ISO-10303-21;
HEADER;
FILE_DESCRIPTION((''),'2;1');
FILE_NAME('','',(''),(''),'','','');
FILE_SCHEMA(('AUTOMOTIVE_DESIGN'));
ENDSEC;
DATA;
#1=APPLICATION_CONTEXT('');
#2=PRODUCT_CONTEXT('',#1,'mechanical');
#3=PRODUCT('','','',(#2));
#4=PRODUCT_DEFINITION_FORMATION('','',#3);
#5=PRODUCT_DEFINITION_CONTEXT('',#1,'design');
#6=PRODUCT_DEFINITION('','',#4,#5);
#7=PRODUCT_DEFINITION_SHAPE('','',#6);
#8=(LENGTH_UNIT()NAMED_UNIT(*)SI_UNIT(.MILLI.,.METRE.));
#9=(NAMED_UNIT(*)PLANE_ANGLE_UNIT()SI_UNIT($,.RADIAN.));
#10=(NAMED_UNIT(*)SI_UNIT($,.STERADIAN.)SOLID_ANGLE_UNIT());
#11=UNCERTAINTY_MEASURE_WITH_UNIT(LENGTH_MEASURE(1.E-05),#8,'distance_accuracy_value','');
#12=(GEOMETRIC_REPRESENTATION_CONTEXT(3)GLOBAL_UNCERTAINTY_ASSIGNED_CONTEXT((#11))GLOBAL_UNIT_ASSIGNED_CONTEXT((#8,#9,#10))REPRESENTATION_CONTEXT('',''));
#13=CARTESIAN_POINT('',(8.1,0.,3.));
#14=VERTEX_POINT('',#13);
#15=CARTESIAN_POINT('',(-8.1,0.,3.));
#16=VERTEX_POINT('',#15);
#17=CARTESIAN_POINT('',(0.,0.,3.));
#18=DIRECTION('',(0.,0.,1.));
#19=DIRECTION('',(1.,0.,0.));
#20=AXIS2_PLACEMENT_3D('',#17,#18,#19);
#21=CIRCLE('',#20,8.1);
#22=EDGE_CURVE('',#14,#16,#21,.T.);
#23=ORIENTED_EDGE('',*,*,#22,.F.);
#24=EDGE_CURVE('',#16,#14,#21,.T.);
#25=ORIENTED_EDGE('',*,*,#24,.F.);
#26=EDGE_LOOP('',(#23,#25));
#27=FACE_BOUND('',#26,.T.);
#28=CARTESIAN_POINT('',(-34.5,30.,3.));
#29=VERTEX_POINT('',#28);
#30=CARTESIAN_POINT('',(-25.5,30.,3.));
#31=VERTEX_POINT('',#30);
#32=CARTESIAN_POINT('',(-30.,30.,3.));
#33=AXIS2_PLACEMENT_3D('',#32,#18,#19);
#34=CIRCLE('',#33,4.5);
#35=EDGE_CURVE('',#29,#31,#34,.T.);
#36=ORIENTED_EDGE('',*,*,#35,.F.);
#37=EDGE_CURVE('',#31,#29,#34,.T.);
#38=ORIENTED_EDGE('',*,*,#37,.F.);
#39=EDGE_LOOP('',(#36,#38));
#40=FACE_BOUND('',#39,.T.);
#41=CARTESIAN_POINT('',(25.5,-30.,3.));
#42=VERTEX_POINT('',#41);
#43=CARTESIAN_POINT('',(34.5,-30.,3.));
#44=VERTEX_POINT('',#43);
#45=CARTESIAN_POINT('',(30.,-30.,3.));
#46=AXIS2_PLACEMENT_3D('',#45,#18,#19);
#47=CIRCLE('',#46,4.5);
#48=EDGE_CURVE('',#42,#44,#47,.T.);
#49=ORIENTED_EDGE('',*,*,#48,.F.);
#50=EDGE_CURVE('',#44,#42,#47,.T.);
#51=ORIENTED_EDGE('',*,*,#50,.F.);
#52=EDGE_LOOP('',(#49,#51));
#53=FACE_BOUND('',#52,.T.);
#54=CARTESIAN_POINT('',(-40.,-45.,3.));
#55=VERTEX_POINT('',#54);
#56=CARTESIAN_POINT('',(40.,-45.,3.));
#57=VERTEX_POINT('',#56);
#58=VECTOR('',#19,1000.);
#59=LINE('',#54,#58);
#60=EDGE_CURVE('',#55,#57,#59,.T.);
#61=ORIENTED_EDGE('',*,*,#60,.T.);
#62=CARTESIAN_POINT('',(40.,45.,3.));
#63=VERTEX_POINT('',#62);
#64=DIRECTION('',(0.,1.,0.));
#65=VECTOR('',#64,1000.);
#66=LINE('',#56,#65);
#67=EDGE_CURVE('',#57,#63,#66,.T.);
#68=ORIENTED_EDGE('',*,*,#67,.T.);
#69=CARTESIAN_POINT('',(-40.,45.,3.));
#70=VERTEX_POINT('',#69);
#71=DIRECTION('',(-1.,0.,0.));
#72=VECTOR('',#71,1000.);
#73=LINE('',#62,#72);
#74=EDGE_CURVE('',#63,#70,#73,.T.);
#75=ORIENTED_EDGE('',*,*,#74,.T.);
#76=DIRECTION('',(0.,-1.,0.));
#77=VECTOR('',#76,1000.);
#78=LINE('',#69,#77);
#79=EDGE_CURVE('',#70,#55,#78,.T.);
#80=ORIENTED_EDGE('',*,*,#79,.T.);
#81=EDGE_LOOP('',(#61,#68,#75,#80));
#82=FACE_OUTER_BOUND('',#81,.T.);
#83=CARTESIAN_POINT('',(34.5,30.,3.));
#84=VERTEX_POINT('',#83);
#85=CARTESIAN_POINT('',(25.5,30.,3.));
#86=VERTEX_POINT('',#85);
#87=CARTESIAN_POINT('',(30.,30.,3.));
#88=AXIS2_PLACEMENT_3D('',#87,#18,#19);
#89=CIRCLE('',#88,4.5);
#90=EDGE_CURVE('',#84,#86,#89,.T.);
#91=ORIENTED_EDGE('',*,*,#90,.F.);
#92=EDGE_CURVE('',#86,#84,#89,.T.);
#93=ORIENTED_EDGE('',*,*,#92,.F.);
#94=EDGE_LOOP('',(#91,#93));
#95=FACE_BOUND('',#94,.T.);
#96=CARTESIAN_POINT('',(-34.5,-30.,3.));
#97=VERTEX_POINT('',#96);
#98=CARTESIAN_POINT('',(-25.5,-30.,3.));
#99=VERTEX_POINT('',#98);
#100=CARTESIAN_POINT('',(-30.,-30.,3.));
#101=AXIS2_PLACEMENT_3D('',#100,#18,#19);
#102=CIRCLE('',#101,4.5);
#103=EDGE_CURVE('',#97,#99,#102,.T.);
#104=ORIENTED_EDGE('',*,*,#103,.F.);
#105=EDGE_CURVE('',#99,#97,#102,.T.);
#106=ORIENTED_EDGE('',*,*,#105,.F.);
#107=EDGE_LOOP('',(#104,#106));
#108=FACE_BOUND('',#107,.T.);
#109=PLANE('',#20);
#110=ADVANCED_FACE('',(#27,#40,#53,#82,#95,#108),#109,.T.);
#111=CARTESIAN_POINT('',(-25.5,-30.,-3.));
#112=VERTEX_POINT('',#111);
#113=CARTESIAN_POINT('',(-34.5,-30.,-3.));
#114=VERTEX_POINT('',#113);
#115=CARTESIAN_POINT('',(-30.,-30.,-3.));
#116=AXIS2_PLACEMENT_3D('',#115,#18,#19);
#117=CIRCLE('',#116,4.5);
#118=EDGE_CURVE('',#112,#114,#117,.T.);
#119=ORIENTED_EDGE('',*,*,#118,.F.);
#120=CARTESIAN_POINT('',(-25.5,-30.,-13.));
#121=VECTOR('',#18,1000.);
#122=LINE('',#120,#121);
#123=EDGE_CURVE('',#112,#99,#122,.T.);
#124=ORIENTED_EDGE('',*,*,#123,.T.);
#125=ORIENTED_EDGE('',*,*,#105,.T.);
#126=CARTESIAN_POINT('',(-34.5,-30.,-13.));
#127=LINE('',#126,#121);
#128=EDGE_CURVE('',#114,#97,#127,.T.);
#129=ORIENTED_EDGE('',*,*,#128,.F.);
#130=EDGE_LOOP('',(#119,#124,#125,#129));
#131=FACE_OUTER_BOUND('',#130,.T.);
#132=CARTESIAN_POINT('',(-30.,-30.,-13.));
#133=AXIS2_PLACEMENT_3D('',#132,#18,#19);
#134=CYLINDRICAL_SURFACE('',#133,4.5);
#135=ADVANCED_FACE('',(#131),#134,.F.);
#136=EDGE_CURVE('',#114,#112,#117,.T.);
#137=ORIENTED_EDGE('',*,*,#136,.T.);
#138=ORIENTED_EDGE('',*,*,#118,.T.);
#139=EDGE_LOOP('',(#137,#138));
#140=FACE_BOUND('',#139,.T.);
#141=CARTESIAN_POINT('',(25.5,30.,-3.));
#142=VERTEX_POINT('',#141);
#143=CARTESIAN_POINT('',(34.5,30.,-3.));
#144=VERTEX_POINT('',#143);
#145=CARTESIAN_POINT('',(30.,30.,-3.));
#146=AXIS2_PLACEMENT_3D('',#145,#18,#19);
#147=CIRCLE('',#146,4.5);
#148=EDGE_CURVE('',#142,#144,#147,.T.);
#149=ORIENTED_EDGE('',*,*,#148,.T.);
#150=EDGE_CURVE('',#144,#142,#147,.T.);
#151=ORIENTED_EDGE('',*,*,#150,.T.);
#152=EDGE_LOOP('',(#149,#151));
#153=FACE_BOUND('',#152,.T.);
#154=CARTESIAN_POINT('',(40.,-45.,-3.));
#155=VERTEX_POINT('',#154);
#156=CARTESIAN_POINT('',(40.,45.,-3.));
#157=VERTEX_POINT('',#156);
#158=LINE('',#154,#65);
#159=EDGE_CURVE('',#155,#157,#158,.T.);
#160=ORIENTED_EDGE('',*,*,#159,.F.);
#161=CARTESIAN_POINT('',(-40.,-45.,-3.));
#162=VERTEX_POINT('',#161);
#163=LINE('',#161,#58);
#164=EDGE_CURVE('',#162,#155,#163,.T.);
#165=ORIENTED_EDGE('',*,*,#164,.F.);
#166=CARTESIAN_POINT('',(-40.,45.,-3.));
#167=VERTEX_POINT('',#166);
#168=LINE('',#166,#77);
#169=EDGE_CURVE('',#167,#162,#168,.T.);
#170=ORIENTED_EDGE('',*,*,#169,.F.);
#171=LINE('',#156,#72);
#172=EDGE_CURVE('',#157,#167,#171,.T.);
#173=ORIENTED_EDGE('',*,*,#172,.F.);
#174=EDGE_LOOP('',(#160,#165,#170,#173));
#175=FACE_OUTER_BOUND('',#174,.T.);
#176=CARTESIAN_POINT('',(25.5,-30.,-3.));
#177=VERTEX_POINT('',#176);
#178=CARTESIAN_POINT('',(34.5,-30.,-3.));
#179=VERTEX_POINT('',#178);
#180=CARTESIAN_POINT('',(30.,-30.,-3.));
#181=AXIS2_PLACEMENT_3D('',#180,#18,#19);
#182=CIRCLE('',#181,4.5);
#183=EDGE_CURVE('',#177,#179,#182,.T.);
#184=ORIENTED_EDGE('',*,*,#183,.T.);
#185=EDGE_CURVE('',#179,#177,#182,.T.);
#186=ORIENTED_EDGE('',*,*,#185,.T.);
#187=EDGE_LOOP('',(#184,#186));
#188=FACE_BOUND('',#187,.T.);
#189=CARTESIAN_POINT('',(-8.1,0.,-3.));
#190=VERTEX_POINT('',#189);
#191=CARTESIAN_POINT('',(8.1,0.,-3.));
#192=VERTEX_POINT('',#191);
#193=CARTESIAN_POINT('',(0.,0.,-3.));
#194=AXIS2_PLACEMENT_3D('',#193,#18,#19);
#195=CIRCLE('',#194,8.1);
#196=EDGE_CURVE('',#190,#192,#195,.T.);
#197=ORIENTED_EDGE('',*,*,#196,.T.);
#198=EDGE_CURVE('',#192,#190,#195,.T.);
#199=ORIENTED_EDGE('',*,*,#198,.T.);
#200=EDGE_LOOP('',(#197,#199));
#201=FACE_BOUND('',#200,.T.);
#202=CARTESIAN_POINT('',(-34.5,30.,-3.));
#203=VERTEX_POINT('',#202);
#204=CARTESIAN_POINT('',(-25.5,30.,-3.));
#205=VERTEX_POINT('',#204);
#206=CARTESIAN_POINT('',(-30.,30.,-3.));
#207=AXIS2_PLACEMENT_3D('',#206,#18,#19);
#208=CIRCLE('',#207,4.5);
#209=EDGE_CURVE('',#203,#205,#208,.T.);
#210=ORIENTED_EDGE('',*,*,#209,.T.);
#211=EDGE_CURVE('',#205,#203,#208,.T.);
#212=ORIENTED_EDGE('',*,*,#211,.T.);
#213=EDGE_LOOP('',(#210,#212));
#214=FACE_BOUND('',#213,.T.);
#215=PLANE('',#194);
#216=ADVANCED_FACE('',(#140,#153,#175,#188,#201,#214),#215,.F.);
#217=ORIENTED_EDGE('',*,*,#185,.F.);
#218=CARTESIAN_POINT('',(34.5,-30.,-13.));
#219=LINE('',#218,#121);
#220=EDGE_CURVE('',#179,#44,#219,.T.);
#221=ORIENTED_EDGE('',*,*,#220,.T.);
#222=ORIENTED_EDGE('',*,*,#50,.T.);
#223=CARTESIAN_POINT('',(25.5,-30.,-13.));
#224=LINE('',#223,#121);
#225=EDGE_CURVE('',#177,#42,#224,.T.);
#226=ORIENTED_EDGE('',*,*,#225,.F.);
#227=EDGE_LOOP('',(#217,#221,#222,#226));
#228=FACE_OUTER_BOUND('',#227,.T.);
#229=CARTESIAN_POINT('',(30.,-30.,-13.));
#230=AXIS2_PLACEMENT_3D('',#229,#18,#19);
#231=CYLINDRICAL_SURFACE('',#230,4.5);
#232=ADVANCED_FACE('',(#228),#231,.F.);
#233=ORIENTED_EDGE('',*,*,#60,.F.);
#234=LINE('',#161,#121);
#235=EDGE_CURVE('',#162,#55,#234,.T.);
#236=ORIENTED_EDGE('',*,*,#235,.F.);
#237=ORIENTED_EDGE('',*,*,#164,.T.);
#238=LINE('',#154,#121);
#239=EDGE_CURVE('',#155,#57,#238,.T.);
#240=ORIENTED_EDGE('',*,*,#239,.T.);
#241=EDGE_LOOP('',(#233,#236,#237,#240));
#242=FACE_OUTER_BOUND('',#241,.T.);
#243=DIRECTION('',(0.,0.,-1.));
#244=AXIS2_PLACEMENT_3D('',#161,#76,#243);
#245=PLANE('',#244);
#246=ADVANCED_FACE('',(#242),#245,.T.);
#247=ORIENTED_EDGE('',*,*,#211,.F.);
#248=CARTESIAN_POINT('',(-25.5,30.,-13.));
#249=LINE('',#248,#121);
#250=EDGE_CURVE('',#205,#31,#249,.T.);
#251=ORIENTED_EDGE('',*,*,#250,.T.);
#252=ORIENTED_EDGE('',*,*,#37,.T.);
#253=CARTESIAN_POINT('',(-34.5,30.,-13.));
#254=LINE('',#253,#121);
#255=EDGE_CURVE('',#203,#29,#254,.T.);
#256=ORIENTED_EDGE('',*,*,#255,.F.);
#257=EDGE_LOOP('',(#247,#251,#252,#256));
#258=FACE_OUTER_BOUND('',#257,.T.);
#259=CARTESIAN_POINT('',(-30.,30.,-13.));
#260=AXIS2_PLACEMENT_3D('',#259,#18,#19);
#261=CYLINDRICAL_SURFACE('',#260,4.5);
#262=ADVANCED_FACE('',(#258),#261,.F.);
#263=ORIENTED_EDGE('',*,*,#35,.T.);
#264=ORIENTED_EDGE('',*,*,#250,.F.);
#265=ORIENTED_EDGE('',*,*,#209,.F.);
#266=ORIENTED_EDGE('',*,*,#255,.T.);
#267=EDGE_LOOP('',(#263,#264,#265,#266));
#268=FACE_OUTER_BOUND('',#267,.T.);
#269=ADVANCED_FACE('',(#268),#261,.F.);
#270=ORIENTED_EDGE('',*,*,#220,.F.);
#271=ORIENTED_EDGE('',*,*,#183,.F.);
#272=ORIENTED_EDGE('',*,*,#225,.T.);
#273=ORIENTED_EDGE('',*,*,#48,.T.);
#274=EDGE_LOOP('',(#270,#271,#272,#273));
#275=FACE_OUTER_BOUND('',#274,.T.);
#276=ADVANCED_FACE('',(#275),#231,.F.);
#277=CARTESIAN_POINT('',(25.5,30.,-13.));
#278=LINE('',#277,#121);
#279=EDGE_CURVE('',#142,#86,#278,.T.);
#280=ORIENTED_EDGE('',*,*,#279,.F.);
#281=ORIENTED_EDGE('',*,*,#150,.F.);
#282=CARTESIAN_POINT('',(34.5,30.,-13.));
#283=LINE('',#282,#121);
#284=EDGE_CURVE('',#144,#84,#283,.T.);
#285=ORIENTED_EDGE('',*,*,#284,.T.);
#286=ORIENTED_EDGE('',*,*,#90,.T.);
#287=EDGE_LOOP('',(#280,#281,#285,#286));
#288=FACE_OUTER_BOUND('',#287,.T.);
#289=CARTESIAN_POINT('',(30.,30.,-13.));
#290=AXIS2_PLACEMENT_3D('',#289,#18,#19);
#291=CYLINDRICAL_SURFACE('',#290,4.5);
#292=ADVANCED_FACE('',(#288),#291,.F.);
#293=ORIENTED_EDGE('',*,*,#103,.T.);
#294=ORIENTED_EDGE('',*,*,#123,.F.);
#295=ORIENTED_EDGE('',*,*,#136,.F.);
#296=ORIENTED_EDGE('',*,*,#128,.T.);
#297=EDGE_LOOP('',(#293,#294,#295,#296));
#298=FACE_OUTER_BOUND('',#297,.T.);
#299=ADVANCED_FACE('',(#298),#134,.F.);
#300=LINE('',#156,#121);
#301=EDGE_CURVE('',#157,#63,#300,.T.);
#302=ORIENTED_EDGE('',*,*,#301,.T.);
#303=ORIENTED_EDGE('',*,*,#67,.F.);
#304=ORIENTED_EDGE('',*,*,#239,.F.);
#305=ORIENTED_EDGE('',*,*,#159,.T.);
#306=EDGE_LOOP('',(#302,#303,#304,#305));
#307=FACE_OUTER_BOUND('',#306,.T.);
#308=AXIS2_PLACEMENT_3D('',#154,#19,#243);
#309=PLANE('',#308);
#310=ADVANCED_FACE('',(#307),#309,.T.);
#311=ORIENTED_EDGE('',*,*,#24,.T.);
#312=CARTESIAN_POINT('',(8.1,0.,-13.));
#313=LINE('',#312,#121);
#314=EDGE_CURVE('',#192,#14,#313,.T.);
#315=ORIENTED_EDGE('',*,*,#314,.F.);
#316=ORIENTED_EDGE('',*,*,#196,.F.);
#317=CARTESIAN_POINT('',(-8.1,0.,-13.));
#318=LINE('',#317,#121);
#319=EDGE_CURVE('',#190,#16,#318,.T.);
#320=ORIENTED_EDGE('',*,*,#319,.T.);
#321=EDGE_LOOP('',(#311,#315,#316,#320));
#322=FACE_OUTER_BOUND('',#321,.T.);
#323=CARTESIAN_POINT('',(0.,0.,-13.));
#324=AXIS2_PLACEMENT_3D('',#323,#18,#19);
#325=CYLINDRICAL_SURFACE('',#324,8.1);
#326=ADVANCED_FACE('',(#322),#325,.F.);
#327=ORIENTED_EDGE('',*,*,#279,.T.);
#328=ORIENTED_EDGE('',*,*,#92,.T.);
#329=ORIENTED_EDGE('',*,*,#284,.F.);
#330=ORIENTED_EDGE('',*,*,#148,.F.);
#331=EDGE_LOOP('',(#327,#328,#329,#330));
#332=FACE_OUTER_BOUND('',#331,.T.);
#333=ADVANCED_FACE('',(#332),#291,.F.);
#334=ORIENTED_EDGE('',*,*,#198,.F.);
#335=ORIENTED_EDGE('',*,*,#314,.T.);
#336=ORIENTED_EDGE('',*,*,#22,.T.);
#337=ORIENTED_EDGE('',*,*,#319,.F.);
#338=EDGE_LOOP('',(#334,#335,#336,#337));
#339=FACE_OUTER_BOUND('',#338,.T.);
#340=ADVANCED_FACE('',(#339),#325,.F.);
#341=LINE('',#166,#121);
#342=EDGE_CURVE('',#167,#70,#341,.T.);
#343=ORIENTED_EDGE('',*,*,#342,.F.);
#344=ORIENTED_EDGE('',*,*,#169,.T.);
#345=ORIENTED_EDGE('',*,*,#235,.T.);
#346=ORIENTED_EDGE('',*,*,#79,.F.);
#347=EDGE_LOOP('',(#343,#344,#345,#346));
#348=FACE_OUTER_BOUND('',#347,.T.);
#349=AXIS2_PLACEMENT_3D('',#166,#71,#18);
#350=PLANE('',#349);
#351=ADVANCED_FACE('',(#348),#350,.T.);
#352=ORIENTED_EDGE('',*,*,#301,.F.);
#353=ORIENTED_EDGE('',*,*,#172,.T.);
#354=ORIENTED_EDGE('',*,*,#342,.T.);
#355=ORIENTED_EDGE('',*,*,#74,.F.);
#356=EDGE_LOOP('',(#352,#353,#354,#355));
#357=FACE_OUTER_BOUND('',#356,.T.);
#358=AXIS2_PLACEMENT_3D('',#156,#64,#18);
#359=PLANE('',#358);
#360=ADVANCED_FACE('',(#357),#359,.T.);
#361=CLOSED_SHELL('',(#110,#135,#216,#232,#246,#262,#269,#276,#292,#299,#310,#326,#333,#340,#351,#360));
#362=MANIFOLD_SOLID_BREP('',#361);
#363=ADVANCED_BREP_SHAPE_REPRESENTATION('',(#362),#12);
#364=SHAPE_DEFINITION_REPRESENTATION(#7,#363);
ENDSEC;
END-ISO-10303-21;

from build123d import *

# Parameters (mm, degrees)
SKETCH_1_W          = 80
SKETCH_1_H          = 90
EXTRUDE_1_DEPTH     = 3
SKETCH_2_R          = 4.5
SKETCH_2_R_2        = 8.1
CUT_EXTRUDE_1_DEPTH = 13


with BuildPart() as part:
    # 草图1 → 凸台-拉伸1 (new, symmetric)
    with BuildSketch(Plane.XY):
        Rectangle(SKETCH_1_W, SKETCH_1_H)
    extrude(amount=EXTRUDE_1_DEPTH, both=True)

    # 草图2 → 切除-拉伸1 (cut, symmetric)
    with BuildSketch(Plane.XY):
        with Locations((-30, -30)):
            Circle(SKETCH_2_R)
        with Locations((-30, 30)):
            Circle(SKETCH_2_R)
        with Locations((30, -30)):
            Circle(SKETCH_2_R)
        with Locations((30, 30)):
            Circle(SKETCH_2_R)
        Circle(SKETCH_2_R_2)
    extrude(amount=CUT_EXTRUDE_1_DEPTH, both=True, mode=Mode.SUBTRACT)


solid = part.part
